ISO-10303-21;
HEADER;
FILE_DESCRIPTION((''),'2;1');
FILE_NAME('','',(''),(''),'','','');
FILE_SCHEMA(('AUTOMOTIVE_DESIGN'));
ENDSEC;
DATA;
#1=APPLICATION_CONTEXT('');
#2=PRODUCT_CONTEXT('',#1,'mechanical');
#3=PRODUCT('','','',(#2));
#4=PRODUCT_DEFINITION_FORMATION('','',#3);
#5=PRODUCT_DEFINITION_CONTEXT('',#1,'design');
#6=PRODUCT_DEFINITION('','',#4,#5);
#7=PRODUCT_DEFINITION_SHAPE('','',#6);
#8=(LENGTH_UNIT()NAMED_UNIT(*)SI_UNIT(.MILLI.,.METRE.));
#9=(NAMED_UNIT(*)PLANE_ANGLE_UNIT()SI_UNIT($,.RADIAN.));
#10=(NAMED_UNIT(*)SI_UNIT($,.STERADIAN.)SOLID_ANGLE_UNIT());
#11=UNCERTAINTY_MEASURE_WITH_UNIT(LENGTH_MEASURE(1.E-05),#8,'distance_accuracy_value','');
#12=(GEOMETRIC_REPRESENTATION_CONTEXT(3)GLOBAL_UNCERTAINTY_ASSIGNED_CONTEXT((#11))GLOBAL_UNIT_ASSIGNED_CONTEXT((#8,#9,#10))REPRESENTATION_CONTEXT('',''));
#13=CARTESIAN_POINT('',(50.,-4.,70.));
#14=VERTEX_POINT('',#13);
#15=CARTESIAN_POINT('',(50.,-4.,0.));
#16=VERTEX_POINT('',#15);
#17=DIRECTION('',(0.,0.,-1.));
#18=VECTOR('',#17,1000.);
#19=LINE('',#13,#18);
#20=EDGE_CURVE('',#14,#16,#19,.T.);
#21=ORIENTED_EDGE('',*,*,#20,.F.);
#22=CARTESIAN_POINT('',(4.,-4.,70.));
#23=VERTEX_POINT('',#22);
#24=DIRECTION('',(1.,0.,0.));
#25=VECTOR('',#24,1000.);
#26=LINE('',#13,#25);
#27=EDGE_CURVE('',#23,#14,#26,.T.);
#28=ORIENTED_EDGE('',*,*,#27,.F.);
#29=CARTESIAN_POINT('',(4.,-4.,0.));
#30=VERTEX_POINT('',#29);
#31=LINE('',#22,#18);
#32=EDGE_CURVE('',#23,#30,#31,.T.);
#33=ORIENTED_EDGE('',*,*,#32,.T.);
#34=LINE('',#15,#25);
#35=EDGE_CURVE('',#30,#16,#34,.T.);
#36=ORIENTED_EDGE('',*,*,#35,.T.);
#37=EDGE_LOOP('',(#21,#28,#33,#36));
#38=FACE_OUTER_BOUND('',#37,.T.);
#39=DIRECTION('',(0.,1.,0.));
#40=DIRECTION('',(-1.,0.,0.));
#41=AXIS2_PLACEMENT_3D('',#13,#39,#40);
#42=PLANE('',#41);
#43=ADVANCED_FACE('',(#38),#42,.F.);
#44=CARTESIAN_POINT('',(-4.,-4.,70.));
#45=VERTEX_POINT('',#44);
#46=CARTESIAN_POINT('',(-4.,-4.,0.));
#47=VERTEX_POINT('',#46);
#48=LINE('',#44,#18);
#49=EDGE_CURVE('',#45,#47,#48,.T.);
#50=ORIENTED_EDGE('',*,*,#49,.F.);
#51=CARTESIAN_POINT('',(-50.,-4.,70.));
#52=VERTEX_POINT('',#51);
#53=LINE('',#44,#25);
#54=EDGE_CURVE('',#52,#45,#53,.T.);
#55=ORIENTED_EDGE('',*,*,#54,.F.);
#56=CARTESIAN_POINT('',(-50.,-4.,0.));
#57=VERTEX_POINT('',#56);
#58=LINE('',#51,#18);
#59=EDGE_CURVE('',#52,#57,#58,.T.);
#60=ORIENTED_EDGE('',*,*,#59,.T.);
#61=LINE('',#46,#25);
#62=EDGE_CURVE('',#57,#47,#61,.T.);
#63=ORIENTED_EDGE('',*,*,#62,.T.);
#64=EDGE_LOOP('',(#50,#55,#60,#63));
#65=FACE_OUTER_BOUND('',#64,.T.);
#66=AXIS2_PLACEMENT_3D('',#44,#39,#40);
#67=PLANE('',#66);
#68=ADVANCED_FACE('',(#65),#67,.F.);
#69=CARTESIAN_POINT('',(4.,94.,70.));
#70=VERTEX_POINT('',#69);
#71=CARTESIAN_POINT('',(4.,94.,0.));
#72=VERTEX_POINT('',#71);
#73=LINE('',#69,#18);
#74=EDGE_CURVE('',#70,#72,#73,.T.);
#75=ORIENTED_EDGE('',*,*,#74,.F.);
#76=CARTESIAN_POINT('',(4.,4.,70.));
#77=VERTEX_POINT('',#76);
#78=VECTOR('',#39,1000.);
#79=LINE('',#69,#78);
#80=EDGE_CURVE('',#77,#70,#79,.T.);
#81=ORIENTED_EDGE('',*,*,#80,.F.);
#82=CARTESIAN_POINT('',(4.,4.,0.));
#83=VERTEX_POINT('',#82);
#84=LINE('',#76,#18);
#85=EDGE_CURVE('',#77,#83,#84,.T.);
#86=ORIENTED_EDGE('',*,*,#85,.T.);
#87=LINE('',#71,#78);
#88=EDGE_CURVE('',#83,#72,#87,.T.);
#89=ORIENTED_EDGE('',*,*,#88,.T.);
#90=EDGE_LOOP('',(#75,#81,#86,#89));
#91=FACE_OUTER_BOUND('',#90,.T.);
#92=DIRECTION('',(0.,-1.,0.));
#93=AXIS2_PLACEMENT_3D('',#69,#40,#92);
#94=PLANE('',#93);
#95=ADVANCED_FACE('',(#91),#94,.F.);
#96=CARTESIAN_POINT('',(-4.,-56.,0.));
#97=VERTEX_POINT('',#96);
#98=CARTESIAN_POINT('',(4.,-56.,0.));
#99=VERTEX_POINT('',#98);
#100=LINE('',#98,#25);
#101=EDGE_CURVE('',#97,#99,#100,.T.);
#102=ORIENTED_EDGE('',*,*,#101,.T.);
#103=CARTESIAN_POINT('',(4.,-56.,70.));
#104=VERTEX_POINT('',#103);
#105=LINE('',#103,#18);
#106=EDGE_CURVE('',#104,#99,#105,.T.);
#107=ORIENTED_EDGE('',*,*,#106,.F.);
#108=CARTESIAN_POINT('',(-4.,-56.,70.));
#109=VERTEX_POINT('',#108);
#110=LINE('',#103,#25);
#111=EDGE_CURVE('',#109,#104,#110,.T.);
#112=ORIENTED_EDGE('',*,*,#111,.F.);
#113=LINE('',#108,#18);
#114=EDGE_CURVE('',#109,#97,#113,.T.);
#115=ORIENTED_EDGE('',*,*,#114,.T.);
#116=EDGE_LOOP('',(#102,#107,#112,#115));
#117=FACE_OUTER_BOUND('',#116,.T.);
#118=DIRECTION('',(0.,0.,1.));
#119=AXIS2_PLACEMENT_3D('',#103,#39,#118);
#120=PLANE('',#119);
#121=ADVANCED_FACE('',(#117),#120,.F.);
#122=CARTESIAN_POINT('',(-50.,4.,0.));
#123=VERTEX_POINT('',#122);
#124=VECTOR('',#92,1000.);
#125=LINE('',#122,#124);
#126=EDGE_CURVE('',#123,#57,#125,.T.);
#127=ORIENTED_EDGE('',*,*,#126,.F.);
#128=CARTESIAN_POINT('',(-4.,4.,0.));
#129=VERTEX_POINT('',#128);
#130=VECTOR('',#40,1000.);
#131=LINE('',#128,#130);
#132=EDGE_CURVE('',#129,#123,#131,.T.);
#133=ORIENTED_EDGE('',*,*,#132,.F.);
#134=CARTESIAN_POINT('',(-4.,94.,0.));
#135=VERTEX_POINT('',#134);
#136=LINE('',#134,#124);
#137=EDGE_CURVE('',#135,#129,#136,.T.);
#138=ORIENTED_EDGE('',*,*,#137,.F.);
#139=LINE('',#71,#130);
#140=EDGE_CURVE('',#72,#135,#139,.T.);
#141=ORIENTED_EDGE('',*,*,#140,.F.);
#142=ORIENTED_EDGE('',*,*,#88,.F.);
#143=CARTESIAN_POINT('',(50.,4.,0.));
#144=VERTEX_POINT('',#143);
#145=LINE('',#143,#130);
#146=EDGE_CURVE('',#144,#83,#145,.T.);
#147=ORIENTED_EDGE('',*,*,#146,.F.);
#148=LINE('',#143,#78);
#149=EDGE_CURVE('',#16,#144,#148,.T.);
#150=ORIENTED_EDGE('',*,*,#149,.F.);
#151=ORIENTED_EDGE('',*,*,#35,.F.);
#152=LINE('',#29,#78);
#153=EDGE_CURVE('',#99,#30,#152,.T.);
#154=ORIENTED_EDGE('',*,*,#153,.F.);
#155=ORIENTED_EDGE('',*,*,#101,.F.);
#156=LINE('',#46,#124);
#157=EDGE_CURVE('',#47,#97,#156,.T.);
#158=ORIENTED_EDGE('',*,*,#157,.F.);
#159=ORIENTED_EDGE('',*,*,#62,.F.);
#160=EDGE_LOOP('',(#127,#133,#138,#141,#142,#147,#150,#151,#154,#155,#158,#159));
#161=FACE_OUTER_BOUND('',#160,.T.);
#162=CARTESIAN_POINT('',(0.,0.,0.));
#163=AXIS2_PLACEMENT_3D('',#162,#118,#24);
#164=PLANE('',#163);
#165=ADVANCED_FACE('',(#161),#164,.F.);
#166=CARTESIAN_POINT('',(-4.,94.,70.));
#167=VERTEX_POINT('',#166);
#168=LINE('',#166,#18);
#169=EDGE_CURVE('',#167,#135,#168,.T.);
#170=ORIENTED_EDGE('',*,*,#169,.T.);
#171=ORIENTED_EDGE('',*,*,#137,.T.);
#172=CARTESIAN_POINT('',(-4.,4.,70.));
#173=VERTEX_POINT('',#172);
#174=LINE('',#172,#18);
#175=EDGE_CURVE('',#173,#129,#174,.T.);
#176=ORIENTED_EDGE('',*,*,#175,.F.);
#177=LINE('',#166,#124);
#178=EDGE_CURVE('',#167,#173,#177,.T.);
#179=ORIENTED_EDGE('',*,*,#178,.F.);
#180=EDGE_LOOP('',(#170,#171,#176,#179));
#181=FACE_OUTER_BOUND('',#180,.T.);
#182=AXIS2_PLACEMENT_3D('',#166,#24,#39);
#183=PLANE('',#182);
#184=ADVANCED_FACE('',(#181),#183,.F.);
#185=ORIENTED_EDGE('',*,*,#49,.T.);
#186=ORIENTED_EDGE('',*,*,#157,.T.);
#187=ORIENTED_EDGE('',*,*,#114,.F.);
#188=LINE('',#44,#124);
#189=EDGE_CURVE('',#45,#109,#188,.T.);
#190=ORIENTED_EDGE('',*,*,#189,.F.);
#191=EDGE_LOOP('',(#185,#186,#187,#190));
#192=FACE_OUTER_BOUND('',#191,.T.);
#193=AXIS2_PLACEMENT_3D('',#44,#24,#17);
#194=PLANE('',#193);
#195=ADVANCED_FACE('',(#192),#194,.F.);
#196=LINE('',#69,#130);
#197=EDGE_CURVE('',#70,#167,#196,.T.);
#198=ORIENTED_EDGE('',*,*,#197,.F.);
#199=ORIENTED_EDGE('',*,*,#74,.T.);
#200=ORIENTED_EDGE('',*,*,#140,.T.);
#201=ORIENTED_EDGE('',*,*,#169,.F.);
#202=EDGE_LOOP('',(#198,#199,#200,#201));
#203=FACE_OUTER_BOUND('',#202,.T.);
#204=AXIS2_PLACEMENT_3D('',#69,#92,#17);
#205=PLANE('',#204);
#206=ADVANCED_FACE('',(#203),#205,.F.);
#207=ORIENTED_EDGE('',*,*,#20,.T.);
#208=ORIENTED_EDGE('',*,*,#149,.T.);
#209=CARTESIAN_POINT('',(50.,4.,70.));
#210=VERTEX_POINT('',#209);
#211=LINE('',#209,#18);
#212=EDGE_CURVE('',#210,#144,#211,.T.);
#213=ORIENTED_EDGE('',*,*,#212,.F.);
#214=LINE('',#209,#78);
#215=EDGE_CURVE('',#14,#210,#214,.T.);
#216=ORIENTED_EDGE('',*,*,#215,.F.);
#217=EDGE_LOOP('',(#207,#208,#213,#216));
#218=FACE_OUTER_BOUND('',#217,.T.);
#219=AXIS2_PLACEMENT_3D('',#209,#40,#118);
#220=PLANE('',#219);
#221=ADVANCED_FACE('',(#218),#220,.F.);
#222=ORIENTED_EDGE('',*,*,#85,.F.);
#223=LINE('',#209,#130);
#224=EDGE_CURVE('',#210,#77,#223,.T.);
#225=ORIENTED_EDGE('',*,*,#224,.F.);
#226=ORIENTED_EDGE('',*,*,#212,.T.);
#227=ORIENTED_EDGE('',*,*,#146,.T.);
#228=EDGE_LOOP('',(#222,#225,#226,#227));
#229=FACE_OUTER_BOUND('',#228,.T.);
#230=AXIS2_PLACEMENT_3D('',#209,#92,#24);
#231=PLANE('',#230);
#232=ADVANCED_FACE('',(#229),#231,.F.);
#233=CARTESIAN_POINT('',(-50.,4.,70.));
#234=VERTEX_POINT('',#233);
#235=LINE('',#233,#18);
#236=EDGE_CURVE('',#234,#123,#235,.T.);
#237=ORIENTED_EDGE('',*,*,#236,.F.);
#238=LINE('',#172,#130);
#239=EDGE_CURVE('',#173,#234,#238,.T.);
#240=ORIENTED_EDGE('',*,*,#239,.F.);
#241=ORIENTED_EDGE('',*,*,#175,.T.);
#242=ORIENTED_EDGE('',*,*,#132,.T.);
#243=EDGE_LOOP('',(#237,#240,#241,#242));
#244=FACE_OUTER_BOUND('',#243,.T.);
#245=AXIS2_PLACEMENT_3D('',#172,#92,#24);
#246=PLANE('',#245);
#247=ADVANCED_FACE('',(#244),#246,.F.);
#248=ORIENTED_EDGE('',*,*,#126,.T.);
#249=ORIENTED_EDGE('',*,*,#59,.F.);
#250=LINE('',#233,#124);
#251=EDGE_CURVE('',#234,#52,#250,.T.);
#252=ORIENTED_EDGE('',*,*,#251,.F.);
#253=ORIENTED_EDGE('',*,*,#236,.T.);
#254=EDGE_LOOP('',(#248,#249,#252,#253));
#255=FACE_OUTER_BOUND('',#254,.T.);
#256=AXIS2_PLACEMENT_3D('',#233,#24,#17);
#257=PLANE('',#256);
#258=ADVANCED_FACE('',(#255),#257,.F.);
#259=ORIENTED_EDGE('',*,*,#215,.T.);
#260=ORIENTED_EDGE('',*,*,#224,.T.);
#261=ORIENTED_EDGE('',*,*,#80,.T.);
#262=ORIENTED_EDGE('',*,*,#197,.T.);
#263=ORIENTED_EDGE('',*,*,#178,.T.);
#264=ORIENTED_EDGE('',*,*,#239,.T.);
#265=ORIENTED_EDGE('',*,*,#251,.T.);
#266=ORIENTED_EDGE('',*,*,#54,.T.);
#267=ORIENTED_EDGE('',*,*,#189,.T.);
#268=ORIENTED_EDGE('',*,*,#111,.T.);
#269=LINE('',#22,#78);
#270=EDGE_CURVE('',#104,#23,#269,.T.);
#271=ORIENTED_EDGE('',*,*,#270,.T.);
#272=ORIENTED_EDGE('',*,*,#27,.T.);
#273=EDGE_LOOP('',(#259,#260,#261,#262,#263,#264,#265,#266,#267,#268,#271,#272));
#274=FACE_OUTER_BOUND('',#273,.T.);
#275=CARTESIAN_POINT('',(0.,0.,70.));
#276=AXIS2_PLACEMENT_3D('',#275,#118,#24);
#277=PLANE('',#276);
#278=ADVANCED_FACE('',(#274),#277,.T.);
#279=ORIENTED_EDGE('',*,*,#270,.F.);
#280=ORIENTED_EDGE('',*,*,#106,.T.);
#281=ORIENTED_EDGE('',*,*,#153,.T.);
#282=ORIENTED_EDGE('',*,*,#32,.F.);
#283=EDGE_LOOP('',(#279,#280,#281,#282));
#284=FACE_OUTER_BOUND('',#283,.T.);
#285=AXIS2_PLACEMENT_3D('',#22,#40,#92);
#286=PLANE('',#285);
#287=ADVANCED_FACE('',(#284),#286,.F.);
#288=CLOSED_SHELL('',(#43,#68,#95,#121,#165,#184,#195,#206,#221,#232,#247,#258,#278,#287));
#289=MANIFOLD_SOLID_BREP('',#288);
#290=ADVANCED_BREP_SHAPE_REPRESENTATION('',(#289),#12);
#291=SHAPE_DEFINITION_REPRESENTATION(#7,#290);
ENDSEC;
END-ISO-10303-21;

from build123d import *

# Parameters (mm, degrees)
BOSS_EXTRUDE1_DEPTH = 70


with BuildPart() as part:
    # Sketch1 → Boss-Extrude1 (new body)
    with BuildSketch(Plane.XY):
        Polygon((4, -4), (4, -56), (-4, -56), (-4, -4), (-50, -4), (-50, 4), (-4, 4), (-4, 94), (4, 94), (4, 4), (50, 4), (50, -4), align=None)
    extrude(amount=BOSS_EXTRUDE1_DEPTH)


solid = part.part
